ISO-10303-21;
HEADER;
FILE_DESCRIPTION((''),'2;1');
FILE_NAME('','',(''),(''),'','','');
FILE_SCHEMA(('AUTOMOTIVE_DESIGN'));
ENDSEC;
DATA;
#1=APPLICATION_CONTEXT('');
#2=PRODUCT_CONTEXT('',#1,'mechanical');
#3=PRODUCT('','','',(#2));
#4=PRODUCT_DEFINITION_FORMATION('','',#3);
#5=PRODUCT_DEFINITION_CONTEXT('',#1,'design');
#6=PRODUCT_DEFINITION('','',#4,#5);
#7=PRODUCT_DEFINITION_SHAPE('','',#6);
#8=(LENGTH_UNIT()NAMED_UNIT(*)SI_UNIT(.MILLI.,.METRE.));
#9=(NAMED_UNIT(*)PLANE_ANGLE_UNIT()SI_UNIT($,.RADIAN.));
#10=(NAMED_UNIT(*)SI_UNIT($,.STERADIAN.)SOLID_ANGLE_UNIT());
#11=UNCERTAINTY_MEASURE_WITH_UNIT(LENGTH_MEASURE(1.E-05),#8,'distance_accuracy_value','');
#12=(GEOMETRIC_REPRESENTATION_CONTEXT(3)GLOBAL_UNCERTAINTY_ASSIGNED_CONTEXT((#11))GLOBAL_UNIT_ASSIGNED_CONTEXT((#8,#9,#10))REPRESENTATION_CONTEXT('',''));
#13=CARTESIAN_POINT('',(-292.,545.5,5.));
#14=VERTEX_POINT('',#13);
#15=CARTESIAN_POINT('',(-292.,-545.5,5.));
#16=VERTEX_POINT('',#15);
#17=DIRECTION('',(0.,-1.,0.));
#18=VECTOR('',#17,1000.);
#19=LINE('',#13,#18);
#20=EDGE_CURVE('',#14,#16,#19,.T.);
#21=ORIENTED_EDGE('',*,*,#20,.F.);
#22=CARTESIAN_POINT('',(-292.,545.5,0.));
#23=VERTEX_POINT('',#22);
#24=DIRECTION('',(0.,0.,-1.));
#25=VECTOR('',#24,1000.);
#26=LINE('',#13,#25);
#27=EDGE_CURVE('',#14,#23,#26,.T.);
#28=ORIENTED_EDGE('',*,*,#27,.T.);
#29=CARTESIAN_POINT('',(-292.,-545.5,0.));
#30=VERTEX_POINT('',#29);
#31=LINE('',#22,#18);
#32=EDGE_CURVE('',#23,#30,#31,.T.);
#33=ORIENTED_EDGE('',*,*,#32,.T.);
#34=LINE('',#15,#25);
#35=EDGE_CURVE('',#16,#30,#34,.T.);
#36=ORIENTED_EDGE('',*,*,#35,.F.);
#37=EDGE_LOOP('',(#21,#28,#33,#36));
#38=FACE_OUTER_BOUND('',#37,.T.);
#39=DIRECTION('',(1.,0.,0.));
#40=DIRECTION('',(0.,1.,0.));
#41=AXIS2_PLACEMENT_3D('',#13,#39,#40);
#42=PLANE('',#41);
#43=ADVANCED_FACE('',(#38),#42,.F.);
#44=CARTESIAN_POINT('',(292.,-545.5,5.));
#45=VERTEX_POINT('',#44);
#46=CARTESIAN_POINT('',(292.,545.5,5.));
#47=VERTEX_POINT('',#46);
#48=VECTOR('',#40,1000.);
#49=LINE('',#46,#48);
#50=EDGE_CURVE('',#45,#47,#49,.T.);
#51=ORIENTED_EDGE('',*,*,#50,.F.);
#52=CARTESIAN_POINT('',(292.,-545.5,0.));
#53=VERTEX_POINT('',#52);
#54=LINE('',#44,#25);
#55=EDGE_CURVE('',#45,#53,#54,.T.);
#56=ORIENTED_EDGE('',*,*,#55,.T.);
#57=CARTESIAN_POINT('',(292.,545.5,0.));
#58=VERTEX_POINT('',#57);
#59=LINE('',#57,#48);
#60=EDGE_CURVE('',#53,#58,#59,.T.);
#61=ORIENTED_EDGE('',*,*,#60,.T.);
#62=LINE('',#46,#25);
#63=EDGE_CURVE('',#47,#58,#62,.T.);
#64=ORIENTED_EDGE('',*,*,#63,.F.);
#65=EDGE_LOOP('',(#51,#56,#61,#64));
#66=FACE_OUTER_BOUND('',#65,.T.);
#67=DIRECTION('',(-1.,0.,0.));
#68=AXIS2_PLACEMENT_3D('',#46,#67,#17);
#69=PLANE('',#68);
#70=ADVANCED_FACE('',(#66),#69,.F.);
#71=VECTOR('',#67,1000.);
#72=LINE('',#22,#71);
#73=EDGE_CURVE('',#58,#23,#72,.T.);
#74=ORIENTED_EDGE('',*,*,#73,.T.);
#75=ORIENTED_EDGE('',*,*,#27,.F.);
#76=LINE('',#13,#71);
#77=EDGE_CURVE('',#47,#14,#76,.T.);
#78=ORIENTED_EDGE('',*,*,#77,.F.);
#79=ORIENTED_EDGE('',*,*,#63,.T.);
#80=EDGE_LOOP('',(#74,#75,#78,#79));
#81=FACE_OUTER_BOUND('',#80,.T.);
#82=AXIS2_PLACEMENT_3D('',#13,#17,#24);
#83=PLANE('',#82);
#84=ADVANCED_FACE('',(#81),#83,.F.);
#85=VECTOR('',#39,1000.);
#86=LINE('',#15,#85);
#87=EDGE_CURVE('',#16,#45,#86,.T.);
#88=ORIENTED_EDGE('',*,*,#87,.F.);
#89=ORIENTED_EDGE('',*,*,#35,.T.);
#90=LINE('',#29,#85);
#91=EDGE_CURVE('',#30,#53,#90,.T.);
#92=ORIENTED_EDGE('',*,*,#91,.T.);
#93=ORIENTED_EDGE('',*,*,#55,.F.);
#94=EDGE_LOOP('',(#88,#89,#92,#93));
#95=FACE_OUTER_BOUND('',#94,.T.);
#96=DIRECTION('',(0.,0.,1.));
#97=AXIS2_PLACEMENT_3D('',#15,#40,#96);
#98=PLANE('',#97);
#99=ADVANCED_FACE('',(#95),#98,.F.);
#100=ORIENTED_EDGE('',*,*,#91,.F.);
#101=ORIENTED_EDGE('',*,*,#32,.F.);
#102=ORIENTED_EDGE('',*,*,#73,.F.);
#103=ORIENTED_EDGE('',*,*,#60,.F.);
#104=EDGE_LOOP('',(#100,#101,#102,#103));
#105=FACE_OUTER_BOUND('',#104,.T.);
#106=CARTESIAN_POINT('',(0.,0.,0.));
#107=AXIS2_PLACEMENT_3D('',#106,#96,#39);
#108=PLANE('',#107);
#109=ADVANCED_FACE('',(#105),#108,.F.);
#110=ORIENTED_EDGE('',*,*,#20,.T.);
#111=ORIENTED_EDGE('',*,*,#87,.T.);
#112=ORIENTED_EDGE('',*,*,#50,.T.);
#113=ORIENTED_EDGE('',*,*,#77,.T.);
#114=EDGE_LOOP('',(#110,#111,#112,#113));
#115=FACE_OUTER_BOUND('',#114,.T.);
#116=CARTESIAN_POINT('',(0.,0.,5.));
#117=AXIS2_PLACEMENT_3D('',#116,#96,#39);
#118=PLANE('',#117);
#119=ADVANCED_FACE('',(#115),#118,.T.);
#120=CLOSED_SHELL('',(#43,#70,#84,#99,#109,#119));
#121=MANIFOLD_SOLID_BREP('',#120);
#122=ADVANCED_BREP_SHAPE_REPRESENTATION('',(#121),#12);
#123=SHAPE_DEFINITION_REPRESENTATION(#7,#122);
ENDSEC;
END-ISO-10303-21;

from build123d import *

# Parameters (mm, degrees)
SKETCH_1_W      = 584
SKETCH_1_H      = 1091
EXTRUDE_1_DEPTH = 5


with BuildPart() as part:
    # 草图1 → 凸台-拉伸1 (new body)
    with BuildSketch(Plane.XY):
        Rectangle(SKETCH_1_W, SKETCH_1_H)
    extrude(amount=EXTRUDE_1_DEPTH)


solid = part.part
